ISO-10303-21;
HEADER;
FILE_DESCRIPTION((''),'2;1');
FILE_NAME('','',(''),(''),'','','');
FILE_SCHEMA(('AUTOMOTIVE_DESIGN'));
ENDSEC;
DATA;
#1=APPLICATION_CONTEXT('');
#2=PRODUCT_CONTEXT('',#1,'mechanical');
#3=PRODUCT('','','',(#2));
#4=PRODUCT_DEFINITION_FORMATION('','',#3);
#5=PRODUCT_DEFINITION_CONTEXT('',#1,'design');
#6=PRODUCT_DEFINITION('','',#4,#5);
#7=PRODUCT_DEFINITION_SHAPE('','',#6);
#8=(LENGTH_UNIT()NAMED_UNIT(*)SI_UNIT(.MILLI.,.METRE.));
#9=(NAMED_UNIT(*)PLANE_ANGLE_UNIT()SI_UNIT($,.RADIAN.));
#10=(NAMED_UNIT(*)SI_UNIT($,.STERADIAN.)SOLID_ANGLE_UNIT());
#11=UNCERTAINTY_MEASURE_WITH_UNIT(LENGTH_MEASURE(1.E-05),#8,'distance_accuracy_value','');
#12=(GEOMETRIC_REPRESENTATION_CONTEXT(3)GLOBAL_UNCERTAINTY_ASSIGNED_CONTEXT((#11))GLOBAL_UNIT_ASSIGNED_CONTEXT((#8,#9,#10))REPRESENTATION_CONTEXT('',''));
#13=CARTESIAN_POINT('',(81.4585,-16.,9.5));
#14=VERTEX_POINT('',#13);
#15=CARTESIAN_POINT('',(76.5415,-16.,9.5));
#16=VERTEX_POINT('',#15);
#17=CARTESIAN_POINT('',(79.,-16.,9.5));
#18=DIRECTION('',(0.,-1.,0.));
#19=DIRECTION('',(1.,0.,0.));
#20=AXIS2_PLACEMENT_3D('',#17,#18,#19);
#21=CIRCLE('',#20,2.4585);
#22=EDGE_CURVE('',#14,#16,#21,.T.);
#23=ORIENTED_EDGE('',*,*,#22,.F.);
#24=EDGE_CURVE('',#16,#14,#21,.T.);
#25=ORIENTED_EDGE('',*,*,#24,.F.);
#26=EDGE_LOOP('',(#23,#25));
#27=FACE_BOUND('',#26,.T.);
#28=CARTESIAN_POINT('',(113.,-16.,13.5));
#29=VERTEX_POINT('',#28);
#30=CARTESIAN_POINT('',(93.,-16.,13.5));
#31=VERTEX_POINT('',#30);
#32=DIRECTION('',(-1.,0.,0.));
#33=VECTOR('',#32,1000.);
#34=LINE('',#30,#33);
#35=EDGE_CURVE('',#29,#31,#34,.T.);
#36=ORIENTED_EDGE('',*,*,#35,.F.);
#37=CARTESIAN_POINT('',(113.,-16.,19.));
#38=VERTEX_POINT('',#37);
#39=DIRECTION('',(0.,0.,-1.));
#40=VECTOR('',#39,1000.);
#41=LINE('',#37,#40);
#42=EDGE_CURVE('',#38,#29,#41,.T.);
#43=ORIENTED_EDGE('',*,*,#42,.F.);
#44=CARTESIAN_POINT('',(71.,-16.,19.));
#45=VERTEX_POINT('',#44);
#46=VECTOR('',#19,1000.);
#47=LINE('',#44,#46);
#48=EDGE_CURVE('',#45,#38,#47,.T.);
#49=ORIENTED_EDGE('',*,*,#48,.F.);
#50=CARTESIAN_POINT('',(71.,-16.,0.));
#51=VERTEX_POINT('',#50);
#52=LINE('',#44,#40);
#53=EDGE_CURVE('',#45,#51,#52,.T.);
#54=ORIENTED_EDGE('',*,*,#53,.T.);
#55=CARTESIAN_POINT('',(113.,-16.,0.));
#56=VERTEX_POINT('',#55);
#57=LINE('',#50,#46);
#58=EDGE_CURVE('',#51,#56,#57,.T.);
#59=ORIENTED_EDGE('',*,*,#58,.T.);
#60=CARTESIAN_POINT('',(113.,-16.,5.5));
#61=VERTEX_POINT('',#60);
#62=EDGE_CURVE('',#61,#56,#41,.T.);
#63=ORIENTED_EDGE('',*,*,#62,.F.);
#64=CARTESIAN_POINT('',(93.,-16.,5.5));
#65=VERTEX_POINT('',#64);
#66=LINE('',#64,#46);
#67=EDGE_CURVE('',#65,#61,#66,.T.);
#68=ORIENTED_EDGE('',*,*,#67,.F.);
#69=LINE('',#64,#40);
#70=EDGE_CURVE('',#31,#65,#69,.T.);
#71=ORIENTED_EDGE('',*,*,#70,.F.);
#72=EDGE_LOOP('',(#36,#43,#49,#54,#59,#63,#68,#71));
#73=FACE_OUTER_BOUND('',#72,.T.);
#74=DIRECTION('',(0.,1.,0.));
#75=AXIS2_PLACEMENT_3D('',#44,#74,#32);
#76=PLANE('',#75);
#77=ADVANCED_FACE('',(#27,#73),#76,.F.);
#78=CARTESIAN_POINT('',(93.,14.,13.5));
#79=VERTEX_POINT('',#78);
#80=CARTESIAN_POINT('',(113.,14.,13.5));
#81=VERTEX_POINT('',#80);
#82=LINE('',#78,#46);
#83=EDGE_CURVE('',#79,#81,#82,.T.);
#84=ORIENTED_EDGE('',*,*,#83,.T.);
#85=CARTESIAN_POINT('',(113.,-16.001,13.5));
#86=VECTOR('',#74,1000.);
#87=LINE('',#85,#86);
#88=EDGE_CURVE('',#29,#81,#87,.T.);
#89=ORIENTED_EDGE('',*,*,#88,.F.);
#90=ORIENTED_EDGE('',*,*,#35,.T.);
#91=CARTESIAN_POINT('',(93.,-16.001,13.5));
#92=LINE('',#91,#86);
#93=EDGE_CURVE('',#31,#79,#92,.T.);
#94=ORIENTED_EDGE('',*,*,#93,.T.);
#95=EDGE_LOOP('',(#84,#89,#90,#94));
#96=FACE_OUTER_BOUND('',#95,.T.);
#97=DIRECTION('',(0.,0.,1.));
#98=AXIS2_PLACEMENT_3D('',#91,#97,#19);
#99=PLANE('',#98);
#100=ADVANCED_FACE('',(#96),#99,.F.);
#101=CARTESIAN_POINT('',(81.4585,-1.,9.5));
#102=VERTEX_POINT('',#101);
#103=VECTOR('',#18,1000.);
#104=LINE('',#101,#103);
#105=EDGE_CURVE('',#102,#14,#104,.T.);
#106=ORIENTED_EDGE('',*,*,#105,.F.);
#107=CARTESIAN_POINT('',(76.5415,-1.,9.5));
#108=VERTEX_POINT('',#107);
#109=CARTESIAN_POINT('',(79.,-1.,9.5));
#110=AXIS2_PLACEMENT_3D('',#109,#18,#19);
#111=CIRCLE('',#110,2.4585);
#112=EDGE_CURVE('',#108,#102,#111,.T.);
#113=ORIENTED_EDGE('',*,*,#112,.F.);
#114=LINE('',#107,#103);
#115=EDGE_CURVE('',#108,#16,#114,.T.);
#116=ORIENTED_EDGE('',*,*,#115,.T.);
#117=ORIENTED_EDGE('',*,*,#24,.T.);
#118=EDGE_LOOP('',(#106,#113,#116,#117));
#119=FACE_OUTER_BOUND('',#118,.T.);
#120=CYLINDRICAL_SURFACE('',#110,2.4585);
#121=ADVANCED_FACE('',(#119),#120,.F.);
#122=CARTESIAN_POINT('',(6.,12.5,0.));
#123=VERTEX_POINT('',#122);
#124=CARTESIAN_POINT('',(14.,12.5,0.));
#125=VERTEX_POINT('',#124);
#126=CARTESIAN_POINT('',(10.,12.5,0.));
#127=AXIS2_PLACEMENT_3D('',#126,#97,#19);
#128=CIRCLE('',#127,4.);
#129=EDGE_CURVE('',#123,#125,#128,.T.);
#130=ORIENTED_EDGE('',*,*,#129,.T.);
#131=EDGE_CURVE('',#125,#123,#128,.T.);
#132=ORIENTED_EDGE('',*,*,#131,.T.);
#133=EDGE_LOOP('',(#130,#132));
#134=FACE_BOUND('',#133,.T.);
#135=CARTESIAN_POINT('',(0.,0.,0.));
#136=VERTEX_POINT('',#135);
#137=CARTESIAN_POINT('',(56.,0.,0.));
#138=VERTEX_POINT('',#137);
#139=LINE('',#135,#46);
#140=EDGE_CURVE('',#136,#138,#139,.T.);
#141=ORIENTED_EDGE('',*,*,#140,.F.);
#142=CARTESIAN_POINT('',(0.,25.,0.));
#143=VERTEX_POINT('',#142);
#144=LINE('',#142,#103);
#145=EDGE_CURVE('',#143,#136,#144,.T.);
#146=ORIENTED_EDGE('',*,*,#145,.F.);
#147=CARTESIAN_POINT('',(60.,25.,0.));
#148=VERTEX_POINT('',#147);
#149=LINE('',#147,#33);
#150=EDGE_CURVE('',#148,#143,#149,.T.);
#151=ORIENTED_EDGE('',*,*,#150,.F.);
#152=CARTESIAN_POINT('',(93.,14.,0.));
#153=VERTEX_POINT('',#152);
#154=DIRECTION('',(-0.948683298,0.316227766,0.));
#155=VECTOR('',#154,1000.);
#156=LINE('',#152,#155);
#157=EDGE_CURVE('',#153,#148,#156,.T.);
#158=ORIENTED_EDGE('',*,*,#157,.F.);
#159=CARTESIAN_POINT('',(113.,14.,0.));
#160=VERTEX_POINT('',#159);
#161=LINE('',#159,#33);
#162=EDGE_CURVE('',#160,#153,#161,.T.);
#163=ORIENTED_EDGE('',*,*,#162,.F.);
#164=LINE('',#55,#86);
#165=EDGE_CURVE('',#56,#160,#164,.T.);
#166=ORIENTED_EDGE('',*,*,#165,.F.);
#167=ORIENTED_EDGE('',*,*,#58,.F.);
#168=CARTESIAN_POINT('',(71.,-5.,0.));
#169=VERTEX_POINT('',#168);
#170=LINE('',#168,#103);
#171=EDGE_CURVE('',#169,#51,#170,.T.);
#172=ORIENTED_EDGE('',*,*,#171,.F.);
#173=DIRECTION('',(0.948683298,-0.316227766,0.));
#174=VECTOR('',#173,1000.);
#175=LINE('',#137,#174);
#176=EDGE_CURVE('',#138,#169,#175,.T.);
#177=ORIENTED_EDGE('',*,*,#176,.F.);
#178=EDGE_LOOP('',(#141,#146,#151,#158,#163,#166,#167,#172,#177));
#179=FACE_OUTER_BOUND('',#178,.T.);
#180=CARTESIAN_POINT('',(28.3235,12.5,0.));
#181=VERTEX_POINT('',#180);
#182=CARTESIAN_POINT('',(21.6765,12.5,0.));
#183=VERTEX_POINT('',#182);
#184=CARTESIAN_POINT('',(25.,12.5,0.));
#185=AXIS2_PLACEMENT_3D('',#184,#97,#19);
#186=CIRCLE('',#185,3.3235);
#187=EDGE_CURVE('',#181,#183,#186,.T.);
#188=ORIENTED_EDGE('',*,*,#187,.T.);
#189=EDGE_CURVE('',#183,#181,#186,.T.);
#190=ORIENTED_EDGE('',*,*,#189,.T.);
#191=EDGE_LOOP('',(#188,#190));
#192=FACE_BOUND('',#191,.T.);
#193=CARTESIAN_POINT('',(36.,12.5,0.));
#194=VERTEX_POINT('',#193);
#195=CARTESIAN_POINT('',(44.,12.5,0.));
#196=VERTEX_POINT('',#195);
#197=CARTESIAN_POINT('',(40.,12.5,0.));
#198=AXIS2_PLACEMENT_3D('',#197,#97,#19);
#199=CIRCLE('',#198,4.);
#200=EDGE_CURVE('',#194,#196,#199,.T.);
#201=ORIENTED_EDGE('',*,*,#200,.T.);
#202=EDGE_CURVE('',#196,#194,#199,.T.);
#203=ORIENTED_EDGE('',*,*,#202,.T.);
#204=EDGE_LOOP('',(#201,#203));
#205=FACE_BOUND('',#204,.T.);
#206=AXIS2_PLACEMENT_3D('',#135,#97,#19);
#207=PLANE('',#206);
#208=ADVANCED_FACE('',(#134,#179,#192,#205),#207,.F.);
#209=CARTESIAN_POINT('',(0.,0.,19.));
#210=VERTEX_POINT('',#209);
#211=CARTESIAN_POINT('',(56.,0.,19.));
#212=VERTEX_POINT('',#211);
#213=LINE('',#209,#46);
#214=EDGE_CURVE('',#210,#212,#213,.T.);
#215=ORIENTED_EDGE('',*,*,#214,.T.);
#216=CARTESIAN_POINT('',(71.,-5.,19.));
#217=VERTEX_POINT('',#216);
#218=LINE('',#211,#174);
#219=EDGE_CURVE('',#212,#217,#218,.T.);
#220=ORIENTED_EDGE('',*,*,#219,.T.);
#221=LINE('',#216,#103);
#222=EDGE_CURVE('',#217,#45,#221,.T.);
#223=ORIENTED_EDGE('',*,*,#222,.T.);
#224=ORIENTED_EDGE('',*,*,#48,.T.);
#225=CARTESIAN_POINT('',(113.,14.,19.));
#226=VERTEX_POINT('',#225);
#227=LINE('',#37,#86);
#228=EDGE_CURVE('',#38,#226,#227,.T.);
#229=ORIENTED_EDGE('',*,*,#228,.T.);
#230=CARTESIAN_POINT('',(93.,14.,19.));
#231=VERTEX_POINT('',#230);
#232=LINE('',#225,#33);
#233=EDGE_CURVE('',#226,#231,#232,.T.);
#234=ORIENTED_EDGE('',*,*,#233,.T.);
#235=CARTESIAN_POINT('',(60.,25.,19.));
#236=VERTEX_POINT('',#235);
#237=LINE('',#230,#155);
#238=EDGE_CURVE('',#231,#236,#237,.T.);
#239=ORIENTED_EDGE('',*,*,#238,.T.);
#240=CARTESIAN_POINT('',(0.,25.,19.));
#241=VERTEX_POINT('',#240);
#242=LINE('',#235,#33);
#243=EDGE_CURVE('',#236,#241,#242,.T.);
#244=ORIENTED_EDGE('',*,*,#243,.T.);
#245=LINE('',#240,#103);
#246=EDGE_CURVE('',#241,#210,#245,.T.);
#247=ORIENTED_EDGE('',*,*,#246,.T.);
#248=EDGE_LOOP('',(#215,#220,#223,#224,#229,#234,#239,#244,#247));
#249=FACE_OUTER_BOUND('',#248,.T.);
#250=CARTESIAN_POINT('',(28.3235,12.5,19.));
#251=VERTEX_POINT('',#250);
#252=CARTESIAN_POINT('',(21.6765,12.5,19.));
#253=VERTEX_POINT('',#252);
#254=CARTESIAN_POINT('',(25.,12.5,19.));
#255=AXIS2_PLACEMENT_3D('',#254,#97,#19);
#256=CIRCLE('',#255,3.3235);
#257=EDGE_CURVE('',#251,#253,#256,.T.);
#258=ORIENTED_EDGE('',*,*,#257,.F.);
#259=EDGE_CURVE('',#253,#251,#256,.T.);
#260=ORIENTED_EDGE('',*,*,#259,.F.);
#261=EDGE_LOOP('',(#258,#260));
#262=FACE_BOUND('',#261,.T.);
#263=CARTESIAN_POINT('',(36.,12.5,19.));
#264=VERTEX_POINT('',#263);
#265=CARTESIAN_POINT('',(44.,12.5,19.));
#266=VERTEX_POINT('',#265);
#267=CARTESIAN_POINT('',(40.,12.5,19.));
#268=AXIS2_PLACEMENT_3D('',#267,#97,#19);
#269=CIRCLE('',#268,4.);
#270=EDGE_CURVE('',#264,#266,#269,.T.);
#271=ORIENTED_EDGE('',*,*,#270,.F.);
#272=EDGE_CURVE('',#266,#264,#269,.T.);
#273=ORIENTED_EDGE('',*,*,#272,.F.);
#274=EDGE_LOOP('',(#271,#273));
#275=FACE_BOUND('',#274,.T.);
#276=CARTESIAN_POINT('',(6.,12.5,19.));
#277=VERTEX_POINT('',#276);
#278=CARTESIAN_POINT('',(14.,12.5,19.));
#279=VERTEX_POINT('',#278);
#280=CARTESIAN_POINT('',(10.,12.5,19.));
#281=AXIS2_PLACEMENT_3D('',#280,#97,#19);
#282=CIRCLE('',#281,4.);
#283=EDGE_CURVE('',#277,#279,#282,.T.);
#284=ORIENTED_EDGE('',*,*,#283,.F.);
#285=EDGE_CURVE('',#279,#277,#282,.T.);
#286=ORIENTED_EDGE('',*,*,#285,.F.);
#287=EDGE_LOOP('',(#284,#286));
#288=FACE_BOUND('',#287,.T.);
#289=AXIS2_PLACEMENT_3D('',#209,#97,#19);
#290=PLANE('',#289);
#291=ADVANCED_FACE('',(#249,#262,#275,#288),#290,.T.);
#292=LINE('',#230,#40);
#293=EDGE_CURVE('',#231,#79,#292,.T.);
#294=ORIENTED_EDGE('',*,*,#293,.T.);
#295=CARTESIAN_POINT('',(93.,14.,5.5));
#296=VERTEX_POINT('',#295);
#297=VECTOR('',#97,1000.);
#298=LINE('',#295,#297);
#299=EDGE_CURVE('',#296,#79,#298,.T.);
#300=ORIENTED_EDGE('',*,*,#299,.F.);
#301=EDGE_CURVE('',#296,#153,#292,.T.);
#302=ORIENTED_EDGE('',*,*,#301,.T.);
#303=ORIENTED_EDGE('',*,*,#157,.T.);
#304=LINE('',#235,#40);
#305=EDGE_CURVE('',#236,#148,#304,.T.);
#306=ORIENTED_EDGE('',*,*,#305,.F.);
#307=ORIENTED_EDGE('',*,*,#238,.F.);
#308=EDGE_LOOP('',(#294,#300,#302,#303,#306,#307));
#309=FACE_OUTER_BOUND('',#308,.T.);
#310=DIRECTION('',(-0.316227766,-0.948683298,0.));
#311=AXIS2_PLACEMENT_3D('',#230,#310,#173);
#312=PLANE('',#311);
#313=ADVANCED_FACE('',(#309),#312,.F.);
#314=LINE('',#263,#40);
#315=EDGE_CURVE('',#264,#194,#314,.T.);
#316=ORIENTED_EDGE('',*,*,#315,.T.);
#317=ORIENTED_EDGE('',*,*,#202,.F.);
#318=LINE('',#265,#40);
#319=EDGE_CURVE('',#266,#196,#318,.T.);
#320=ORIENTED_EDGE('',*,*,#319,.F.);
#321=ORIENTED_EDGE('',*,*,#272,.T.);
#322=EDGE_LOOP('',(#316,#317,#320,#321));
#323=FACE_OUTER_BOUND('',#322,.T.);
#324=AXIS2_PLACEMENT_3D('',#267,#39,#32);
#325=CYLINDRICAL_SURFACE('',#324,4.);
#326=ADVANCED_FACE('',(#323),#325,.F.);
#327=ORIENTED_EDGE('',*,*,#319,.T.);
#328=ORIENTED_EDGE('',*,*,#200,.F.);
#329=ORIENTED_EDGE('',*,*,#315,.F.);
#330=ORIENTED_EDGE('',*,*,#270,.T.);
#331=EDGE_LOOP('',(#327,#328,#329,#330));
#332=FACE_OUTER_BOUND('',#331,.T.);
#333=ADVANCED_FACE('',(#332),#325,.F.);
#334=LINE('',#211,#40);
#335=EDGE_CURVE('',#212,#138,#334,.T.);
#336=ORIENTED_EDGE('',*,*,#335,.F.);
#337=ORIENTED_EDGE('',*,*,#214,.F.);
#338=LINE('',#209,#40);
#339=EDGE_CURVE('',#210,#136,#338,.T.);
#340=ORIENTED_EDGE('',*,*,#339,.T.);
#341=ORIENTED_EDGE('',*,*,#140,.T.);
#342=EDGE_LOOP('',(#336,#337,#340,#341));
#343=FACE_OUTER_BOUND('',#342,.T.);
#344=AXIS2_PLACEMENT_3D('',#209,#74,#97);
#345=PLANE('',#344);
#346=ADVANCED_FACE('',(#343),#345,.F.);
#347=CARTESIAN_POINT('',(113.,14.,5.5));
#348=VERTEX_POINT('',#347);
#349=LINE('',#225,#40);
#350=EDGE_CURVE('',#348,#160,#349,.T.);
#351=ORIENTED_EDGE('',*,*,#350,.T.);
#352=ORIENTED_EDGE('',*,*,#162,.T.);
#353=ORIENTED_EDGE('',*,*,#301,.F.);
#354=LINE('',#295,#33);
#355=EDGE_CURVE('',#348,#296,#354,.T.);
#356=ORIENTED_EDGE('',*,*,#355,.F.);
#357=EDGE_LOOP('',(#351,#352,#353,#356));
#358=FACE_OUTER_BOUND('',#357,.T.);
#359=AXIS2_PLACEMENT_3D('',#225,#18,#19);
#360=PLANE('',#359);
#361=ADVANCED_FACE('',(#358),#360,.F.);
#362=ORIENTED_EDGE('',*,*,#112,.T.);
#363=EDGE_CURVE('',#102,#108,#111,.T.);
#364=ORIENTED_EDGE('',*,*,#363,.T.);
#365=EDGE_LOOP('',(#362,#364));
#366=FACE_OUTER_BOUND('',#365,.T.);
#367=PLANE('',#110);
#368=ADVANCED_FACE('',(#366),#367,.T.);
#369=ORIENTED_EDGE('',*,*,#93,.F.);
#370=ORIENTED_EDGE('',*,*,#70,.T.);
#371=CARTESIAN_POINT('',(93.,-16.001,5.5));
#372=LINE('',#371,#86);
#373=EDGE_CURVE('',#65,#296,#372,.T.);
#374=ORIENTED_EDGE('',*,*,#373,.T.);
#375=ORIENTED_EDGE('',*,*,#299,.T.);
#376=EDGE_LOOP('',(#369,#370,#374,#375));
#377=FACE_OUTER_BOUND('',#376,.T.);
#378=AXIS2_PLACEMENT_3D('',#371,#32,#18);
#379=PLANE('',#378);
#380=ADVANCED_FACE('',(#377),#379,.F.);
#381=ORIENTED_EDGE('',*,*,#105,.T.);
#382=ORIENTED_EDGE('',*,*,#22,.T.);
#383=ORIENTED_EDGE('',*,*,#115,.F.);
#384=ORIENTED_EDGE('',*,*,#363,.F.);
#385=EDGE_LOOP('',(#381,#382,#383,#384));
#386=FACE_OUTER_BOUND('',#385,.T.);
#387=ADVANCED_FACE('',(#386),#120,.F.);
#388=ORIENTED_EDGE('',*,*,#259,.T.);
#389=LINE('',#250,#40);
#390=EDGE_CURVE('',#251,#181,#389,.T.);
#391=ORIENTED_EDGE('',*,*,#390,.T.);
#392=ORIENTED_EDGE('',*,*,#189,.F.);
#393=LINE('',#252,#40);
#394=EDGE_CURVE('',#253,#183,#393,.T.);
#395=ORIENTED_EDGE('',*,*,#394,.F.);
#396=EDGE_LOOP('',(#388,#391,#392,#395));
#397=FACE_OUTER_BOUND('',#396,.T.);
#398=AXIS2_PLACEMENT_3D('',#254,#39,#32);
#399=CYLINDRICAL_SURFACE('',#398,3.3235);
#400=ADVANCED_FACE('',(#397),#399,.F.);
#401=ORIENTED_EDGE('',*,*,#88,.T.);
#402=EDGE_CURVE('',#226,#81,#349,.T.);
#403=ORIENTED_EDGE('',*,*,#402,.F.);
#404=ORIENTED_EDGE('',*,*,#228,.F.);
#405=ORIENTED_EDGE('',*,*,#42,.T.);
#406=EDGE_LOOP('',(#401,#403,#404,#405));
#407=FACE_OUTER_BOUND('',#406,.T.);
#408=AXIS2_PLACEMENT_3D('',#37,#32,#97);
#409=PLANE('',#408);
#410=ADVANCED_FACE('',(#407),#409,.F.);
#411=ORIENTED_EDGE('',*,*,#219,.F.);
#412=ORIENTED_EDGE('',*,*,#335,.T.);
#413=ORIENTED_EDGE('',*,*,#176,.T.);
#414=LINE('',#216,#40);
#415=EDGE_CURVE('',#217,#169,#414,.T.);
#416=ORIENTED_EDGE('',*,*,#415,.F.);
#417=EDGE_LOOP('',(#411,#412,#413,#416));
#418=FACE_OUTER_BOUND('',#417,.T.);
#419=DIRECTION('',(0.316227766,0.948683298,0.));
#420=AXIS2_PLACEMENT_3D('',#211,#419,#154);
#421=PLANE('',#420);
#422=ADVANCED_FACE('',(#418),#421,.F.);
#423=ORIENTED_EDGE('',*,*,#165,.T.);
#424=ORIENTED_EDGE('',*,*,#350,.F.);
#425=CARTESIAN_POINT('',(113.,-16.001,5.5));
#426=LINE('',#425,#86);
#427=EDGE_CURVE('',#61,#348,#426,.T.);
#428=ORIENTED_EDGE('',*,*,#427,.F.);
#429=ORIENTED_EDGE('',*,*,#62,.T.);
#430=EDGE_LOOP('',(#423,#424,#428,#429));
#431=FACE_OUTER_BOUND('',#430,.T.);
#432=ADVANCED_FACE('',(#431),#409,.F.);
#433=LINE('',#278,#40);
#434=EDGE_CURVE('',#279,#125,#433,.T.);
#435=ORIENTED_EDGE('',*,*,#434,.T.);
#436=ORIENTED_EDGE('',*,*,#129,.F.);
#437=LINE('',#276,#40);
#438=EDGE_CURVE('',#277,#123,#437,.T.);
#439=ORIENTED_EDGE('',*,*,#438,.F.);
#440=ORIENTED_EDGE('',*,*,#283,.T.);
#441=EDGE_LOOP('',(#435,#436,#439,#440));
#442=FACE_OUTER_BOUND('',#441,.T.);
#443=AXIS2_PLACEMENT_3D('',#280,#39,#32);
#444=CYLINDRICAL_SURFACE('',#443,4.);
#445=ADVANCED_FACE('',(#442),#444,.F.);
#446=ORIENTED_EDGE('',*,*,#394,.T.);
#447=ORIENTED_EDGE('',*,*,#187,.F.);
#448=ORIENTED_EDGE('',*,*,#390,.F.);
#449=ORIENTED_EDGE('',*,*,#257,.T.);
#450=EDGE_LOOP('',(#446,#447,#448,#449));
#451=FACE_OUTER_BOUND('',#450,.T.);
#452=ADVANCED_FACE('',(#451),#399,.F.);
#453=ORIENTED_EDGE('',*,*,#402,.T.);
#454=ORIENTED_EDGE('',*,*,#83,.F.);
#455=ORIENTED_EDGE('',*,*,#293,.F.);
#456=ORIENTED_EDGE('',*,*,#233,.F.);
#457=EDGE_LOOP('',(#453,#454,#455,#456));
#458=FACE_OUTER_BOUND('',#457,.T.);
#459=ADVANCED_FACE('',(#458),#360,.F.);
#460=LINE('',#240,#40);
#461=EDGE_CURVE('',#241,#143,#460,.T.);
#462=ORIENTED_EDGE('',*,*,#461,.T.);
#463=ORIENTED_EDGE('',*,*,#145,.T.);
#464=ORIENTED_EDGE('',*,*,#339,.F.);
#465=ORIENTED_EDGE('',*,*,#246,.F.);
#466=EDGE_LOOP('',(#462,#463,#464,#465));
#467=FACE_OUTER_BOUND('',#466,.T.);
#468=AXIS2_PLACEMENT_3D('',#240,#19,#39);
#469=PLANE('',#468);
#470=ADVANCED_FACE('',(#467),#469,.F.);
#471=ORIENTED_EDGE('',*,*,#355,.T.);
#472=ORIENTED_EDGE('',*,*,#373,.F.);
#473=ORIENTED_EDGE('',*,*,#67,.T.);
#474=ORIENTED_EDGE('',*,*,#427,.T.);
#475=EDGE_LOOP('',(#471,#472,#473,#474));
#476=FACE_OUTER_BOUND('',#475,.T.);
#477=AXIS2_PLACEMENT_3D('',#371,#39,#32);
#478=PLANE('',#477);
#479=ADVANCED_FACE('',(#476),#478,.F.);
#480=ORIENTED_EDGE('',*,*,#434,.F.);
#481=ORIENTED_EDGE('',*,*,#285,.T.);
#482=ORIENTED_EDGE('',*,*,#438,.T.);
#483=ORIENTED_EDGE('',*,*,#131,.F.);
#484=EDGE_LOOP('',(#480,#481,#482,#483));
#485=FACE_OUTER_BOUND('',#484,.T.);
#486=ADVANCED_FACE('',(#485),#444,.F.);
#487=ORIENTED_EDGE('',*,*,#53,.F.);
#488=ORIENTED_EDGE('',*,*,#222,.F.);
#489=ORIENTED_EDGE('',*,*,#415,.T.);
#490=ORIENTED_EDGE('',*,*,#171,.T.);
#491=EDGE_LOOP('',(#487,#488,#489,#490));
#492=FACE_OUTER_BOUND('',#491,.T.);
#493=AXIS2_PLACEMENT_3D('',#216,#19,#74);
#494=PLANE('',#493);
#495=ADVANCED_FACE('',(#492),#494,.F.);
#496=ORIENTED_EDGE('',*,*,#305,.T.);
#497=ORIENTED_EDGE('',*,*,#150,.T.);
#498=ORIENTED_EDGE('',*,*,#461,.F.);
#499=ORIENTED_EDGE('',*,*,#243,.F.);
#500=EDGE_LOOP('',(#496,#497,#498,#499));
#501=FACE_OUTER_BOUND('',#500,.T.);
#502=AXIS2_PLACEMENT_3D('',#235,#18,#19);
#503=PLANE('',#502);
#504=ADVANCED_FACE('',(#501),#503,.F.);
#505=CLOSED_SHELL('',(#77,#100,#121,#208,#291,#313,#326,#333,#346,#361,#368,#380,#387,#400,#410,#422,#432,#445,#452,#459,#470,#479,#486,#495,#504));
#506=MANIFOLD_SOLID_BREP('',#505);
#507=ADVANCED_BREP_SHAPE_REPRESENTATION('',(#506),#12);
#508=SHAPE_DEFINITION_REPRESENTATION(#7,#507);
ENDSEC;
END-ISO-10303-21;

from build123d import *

# Parameters (mm, degrees)
SKETCH1_R           = 4
SKETCH1_R_2         = 3.3235
BOSS_EXTRUDE1_DEPTH = 19
CUT_EXTRUDE1_REACH  = 120.448
SKETCH2_W           = 20
SKETCH2_H           = 8
SKETCH3_R           = 2.4585
CUT_EXTRUDE2_DEPTH  = 15


with BuildPart() as part:
    # Sketch1 → Boss-Extrude1 (new body)
    with BuildSketch(Plane.XY):
        Polygon((0, 0), (56, 0), (71, -5), (71, -16), (113, -16), (113, 14), (93, 14), (60, 25), (0, 25), align=None)
        with Locations((10, 12.5)):
            Circle(SKETCH1_R, mode=Mode.SUBTRACT)
        with Locations((25, 12.5)):
            Circle(SKETCH1_R_2, mode=Mode.SUBTRACT)
        with Locations((40, 12.5)):
            Circle(SKETCH1_R, mode=Mode.SUBTRACT)
    extrude(amount=BOSS_EXTRUDE1_DEPTH)

    # Sketch2 → Cut-Extrude1 (cut, up to next)
    with BuildSketch(Plane(origin=(0, 14, 0), x_dir=(1, 0, 0), z_dir=(0, 1, 0)), mode=Mode.PRIVATE) as cut_extrude1_sk1:
        with Locations((103, -9.5)):
            Rectangle(SKETCH2_W, SKETCH2_H)
    cut_extrude1_tool1 = extrude(cut_extrude1_sk1.sketch, amount=-CUT_EXTRUDE1_REACH, mode=Mode.PRIVATE) & part.part
    add(cut_extrude1_tool1.solids().sort_by_distance((103, 14, 9.5))[0], mode=Mode.SUBTRACT)

    # Sketch3 → Cut-Extrude2 (cut)
    with BuildSketch(Plane(origin=(0, -16, 0), x_dir=(-1, 0, 0), z_dir=(0, -1, 0))):
        with Locations(Location((-79, -9.5, 0), (0, 0, 180))):
            Circle(SKETCH3_R)
    extrude(amount=-CUT_EXTRUDE2_DEPTH, mode=Mode.SUBTRACT)


solid = part.part
